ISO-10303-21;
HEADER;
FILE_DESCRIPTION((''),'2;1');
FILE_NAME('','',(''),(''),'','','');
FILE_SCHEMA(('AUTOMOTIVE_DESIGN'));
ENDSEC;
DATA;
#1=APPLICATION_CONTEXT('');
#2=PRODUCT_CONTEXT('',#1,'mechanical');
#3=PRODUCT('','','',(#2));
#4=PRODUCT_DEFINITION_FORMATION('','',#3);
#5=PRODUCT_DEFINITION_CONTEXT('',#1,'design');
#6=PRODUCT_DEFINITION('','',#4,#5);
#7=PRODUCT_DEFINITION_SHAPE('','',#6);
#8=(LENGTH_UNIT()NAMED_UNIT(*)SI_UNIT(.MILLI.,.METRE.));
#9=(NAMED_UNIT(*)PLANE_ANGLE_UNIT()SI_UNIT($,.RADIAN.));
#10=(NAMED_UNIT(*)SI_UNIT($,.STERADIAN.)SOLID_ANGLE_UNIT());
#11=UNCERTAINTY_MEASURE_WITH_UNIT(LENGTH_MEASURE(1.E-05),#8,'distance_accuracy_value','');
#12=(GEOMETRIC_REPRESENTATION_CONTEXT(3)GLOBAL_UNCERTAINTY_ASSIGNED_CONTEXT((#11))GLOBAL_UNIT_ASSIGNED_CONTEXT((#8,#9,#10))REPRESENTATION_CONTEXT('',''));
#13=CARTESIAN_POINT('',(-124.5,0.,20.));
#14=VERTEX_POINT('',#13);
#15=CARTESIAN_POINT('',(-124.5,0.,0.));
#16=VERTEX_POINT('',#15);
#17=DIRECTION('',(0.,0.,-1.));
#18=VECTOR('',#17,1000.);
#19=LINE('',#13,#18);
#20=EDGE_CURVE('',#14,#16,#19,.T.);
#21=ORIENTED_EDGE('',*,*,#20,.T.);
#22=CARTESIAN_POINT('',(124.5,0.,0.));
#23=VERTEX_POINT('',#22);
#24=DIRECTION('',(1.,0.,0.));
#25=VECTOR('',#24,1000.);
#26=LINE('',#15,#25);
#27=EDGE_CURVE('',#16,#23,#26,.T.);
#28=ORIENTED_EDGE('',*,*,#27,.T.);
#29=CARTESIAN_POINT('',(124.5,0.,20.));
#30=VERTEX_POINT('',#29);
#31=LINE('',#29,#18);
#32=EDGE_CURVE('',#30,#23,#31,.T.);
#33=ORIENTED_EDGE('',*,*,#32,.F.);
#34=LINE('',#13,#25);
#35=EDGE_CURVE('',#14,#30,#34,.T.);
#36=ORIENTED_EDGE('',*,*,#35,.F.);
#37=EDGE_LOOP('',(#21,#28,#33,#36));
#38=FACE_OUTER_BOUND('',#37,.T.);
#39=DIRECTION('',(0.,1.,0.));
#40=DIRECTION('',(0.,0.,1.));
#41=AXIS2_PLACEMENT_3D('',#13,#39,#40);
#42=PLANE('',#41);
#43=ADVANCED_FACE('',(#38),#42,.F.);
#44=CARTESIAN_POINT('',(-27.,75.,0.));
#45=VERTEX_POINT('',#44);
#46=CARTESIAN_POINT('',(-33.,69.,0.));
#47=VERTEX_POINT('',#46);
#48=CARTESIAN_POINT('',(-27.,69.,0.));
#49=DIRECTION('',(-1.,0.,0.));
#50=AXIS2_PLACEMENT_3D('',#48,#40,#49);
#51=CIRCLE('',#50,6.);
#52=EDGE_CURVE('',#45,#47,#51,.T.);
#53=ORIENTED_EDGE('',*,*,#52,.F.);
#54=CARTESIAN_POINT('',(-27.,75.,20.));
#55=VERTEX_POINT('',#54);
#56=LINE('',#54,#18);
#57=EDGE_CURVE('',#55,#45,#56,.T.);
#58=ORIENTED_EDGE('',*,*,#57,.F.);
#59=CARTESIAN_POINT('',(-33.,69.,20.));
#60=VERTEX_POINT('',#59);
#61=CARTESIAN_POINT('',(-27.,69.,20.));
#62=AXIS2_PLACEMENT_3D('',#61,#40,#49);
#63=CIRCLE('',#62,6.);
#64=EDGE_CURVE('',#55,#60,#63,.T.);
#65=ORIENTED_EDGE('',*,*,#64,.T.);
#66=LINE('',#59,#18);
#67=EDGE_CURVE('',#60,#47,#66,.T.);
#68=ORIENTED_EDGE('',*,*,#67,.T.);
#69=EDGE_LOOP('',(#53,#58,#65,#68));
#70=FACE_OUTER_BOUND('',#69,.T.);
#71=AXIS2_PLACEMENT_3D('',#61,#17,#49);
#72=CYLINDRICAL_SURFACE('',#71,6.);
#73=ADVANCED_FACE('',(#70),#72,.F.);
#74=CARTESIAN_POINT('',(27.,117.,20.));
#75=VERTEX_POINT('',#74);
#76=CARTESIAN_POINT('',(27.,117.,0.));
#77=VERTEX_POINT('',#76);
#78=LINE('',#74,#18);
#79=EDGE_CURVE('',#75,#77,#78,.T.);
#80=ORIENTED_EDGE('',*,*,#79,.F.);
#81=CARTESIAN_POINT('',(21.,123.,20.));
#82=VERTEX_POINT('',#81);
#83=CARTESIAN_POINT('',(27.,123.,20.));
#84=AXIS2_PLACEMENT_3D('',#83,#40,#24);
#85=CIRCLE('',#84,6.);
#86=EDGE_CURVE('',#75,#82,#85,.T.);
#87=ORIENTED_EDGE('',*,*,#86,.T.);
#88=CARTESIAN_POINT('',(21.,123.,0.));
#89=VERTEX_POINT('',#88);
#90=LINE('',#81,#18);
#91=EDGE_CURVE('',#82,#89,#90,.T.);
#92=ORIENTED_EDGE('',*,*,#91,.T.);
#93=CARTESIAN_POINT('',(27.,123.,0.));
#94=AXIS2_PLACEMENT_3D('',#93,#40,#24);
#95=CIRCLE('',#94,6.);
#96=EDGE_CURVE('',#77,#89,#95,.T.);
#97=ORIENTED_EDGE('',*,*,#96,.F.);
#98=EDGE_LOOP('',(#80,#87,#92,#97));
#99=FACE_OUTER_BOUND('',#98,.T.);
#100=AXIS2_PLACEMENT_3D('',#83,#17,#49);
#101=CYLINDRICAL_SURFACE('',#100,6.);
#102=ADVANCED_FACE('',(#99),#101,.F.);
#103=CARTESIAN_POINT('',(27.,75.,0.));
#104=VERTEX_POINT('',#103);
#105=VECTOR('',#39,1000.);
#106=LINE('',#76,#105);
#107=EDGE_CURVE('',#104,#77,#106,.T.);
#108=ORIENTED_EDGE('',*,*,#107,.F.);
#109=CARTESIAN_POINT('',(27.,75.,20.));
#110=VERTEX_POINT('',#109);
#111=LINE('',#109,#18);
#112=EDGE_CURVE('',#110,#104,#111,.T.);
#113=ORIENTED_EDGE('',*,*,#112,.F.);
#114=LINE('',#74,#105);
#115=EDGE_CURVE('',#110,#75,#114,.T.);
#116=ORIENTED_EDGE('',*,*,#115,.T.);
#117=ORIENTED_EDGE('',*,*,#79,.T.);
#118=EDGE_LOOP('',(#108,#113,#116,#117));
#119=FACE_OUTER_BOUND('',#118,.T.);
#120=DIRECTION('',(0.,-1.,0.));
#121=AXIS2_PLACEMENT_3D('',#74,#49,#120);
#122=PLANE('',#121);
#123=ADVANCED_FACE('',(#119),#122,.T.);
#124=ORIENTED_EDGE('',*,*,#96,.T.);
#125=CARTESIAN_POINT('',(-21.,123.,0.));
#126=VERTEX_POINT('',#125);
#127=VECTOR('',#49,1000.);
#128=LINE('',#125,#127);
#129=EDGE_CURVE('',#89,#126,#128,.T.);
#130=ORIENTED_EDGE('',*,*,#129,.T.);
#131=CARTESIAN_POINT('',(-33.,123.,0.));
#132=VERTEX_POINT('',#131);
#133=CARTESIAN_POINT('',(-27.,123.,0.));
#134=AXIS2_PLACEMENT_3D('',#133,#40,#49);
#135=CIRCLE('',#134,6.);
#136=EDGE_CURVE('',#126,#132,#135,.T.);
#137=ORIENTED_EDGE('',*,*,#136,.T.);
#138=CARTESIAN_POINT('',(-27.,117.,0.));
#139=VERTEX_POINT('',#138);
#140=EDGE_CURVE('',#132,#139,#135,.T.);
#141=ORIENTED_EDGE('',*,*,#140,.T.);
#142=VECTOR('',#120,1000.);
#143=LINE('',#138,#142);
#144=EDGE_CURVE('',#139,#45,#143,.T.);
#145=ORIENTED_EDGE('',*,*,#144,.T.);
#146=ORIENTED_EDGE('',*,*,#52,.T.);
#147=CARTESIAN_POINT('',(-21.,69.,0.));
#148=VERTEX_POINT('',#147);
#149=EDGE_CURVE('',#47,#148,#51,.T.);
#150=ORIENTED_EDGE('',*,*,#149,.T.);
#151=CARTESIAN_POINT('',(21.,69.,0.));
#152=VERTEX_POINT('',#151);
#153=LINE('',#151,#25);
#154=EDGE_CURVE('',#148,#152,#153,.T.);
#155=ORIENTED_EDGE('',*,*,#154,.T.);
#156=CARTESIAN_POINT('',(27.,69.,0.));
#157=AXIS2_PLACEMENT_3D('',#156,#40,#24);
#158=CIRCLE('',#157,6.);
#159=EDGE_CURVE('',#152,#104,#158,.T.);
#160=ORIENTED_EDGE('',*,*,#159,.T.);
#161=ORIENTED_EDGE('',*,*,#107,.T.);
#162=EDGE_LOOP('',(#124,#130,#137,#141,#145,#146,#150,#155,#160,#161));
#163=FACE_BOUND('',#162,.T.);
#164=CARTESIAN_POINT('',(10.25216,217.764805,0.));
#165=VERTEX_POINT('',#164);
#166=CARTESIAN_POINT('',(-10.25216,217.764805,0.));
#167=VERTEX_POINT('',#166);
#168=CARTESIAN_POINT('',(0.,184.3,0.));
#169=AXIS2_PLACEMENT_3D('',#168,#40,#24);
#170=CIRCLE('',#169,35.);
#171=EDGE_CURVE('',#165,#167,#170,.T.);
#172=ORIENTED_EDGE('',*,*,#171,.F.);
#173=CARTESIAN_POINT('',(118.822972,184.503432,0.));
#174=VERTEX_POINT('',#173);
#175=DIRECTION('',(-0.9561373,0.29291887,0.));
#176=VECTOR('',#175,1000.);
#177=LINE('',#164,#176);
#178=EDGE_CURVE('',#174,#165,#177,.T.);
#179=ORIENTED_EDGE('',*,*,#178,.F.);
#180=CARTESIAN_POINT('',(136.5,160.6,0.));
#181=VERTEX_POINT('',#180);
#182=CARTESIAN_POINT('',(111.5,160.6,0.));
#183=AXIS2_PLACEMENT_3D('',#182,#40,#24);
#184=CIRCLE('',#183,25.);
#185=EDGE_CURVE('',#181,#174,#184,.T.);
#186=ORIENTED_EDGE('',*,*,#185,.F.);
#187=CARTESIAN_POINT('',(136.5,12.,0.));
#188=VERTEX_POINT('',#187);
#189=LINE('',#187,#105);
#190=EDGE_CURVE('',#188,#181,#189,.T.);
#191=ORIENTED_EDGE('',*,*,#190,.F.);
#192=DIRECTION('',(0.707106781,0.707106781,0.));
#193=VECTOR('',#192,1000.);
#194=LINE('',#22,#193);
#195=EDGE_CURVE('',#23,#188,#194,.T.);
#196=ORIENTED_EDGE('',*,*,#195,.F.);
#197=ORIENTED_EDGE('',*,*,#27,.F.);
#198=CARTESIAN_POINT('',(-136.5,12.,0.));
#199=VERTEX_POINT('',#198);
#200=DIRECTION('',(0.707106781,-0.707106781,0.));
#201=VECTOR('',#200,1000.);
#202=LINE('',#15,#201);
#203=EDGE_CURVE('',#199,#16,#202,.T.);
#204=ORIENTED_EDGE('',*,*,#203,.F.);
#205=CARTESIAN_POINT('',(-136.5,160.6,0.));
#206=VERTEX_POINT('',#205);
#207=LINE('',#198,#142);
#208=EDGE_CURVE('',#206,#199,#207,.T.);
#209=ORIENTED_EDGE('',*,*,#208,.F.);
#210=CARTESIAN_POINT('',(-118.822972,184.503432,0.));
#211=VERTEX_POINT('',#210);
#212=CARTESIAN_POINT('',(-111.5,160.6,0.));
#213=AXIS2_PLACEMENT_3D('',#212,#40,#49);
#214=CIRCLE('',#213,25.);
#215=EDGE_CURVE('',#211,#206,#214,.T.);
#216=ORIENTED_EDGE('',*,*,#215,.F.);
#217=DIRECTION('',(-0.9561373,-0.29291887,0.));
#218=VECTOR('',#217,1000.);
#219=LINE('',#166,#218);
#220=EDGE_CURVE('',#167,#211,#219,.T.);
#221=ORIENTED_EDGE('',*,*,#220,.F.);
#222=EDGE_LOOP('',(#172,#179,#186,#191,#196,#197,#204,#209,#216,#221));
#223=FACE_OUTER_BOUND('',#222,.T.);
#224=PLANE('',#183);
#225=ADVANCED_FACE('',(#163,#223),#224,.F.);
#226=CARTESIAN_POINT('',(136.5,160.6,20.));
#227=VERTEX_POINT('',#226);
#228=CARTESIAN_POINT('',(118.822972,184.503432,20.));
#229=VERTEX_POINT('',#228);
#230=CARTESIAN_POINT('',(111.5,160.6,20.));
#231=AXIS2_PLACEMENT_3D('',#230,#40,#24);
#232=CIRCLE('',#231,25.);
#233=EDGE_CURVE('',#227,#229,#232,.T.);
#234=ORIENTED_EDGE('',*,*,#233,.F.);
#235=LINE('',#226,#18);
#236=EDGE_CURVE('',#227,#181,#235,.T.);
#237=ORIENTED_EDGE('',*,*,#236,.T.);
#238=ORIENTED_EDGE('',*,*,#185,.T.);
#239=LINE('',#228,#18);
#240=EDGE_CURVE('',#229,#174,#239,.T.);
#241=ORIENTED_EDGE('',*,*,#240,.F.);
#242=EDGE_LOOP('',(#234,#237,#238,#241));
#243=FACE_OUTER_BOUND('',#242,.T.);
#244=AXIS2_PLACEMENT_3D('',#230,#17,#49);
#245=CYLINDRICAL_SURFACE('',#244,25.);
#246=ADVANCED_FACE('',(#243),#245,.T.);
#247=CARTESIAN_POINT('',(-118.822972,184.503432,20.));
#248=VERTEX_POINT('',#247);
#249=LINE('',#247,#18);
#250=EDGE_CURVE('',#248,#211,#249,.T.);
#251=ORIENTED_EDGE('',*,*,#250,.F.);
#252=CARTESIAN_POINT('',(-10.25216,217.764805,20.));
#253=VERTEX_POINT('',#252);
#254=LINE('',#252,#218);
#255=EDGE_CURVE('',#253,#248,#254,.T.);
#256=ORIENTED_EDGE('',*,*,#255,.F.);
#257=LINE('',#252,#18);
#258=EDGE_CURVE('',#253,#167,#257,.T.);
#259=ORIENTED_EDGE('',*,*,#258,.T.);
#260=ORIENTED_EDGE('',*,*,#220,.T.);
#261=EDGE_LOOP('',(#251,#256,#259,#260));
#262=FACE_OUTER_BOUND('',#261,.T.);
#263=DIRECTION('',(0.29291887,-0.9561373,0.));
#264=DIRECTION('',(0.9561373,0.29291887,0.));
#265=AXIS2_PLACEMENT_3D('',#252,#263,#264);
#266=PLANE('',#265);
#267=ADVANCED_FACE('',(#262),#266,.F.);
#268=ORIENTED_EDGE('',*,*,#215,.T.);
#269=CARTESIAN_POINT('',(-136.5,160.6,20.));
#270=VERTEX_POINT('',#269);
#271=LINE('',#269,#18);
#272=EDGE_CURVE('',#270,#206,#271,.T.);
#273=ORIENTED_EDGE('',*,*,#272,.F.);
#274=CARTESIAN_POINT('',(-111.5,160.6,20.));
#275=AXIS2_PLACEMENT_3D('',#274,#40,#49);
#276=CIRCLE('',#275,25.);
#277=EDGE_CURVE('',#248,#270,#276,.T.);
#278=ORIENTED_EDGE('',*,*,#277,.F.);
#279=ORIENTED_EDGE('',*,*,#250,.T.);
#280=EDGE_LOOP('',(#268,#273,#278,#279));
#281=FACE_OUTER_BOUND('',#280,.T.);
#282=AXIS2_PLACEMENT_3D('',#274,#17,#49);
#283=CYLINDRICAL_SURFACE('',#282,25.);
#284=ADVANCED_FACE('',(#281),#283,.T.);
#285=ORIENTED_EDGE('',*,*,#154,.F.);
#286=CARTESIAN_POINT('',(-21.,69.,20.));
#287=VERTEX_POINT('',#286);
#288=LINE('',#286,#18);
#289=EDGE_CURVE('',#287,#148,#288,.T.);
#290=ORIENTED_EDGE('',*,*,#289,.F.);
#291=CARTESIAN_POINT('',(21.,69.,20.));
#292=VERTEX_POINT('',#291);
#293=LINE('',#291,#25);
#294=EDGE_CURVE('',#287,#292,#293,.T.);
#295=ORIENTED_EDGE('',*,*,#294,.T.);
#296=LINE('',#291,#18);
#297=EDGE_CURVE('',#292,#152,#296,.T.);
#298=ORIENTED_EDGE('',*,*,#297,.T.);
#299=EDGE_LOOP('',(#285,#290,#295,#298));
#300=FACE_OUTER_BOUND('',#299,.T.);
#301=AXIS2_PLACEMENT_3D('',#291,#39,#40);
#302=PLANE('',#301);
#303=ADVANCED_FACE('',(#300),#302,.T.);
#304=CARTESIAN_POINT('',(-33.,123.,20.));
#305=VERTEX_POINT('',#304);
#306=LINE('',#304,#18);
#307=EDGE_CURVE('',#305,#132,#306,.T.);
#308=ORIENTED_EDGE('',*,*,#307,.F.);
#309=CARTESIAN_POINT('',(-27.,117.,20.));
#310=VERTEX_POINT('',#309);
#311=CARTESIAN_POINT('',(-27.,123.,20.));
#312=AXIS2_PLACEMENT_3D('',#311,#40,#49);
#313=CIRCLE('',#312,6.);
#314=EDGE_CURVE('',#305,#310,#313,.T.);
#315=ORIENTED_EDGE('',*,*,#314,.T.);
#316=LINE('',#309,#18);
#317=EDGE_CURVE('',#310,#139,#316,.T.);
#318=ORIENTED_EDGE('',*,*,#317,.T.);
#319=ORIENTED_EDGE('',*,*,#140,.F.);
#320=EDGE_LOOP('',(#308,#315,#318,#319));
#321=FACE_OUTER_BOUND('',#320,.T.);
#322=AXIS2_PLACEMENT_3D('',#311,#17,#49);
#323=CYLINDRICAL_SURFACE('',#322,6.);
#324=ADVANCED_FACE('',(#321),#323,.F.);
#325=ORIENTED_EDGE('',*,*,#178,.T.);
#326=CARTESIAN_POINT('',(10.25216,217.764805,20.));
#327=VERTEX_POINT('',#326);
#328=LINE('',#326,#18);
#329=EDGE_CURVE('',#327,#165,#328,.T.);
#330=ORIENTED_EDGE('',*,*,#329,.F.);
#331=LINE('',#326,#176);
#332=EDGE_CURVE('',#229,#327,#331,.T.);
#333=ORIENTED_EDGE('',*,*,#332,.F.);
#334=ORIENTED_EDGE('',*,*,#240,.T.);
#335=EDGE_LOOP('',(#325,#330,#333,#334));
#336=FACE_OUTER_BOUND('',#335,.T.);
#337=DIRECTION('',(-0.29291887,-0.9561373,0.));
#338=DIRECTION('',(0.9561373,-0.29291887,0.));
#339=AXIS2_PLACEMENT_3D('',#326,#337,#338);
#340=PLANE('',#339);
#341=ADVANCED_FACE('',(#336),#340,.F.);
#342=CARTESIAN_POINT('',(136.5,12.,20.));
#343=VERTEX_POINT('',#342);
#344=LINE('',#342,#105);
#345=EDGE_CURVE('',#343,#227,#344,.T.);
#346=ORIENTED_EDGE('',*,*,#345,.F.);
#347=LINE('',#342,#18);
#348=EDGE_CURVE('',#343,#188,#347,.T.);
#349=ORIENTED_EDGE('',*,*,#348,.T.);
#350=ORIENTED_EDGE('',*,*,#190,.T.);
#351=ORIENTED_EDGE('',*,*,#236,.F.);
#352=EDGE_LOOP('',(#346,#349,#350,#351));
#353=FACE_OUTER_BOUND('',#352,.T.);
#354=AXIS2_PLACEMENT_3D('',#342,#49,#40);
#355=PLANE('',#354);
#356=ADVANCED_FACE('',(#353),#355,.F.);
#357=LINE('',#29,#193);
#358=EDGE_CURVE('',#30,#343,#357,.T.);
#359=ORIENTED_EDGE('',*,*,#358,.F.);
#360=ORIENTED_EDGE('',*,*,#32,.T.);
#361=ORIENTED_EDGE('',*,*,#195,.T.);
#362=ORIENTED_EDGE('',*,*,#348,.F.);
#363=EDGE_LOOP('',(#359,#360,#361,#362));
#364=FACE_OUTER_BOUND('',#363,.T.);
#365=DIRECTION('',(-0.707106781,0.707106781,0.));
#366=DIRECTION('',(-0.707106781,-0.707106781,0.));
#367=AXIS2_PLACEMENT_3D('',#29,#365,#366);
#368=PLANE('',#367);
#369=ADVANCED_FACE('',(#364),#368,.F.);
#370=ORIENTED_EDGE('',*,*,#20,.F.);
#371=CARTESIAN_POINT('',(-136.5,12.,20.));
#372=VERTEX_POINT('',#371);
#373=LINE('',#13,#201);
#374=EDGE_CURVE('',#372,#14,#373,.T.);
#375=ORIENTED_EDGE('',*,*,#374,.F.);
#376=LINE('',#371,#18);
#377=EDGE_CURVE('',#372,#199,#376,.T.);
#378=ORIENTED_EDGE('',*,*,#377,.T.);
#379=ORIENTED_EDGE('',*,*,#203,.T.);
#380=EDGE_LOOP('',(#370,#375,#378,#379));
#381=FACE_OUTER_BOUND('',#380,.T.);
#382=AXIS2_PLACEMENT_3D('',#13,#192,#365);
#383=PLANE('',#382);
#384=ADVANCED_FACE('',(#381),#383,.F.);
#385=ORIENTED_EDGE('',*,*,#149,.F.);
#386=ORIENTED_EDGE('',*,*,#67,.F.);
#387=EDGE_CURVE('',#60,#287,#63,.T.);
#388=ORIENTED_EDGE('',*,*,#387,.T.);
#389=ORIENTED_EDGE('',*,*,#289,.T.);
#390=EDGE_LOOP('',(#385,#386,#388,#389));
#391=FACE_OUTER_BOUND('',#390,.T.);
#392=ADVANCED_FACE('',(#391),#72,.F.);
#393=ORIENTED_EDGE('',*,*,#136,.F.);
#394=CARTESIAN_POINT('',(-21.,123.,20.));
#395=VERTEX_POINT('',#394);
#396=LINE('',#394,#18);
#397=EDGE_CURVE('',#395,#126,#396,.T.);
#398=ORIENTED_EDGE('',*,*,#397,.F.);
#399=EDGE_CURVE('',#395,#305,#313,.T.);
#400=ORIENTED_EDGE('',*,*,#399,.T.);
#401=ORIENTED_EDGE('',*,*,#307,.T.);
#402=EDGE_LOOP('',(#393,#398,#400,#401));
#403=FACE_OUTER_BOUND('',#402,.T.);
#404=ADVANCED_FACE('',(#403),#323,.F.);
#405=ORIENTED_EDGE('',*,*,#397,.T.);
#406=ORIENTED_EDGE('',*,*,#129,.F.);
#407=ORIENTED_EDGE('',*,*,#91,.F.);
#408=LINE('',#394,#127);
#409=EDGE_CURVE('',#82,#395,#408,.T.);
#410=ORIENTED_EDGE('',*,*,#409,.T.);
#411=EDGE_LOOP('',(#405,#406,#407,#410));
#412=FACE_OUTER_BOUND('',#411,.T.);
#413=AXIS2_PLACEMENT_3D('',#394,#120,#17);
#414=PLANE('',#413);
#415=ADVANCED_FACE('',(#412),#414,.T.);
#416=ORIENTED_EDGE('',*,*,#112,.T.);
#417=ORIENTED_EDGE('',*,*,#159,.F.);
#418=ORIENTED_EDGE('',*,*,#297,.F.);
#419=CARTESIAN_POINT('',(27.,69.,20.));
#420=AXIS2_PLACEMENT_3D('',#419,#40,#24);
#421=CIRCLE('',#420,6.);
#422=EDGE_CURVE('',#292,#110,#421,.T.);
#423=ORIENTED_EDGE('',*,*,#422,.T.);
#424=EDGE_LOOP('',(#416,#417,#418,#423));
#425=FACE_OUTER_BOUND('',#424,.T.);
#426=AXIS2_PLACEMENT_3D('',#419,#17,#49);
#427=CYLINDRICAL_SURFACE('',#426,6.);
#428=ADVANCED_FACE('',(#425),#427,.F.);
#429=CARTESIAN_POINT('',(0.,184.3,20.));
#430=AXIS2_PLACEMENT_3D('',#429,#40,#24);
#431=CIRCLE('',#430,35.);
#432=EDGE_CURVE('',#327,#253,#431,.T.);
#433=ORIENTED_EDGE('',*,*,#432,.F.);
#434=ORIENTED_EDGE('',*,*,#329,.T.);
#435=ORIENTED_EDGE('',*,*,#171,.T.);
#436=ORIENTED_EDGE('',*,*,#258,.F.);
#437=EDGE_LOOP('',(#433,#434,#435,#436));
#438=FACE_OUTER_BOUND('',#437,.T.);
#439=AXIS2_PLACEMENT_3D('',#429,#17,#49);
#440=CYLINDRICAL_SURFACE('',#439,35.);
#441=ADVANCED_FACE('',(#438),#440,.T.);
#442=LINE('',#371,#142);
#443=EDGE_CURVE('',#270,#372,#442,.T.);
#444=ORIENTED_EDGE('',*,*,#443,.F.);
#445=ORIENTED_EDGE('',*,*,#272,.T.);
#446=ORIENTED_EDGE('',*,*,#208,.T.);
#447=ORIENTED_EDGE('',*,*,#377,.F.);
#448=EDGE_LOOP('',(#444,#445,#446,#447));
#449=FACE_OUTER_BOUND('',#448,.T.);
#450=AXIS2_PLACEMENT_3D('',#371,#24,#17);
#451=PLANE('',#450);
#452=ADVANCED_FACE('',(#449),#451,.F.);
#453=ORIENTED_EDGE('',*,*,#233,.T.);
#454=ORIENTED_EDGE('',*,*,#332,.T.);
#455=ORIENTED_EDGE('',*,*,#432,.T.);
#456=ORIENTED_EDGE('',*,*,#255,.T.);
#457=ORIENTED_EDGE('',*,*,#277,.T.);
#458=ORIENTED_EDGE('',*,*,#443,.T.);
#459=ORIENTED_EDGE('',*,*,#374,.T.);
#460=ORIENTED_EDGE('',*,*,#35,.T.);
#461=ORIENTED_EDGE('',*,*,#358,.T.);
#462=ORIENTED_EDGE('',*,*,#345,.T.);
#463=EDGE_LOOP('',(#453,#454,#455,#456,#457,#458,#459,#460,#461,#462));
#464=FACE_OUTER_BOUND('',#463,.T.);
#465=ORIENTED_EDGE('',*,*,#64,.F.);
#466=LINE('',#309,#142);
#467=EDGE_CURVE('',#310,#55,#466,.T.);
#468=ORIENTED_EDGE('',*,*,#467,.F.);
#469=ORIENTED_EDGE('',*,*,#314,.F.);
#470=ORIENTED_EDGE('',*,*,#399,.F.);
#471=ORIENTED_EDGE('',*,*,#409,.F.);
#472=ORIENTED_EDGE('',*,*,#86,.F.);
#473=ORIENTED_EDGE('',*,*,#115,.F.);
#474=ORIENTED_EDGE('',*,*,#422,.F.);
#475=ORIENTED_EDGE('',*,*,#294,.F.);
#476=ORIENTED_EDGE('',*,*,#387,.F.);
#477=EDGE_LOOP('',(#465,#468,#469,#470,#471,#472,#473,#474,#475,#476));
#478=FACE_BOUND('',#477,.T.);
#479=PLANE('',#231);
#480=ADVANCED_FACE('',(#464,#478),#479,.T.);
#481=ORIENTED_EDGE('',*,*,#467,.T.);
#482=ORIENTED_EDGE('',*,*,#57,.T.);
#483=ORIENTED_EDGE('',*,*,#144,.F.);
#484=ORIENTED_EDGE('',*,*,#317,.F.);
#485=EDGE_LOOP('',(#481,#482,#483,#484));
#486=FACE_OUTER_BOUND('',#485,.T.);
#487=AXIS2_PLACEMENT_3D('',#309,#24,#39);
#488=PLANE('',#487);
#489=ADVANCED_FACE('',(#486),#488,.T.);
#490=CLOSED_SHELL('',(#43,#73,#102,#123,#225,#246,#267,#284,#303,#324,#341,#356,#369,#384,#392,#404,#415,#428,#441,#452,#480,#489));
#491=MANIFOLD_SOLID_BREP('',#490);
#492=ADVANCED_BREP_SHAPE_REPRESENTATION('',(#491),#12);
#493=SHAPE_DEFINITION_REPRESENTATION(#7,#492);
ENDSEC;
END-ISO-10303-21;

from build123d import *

# Parameters (mm, degrees)
BOSS_EXTRUDE1_DEPTH = 20


with BuildPart() as part:
    # Sketch1 → Boss-Extrude1 (new body)
    with BuildSketch(Plane.XY):
        with BuildLine():
            Line((-124.5, 0), (124.5, 0))
            Line((124.5, 0), (136.5, 12))
            Line((136.5, 12), (136.5, 160.6))
            ThreePointArc((136.5, 160.6), (131.600675284, 175.464819311), (118.822971749, 184.503432489))
            Line((118.822971749, 184.503432489), (10.252160448, 217.764805485))
            ThreePointArc((10.252160448, 217.764805485), (0, 219.3), (-10.252160448, 217.764805485))
            Line((-10.252160448, 217.764805485), (-118.822971749, 184.503432489))
            ThreePointArc((-118.822971749, 184.503432489), (-131.600675284, 175.464819311), (-136.5, 160.6))
            Line((-136.5, 160.6), (-136.5, 12))
            Line((-136.5, 12), (-124.5, 0))
        make_face()
        with BuildLine():
            Line((-21, 123), (21, 123))
            ThreePointArc((21, 123), (31.242640687, 127.242640687), (27, 117))
            Line((27, 117), (27, 75))
            ThreePointArc((27, 75), (31.242640687, 64.757359313), (21, 69))
            Line((21, 69), (-21, 69))
            ThreePointArc((-21, 69), (-31.242640687, 64.757359313), (-27, 75))
            Line((-27, 75), (-27, 117))
            ThreePointArc((-27, 117), (-31.242640687, 127.242640687), (-21, 123))
        make_face(mode=Mode.SUBTRACT)
    extrude(amount=BOSS_EXTRUDE1_DEPTH)


solid = part.part
